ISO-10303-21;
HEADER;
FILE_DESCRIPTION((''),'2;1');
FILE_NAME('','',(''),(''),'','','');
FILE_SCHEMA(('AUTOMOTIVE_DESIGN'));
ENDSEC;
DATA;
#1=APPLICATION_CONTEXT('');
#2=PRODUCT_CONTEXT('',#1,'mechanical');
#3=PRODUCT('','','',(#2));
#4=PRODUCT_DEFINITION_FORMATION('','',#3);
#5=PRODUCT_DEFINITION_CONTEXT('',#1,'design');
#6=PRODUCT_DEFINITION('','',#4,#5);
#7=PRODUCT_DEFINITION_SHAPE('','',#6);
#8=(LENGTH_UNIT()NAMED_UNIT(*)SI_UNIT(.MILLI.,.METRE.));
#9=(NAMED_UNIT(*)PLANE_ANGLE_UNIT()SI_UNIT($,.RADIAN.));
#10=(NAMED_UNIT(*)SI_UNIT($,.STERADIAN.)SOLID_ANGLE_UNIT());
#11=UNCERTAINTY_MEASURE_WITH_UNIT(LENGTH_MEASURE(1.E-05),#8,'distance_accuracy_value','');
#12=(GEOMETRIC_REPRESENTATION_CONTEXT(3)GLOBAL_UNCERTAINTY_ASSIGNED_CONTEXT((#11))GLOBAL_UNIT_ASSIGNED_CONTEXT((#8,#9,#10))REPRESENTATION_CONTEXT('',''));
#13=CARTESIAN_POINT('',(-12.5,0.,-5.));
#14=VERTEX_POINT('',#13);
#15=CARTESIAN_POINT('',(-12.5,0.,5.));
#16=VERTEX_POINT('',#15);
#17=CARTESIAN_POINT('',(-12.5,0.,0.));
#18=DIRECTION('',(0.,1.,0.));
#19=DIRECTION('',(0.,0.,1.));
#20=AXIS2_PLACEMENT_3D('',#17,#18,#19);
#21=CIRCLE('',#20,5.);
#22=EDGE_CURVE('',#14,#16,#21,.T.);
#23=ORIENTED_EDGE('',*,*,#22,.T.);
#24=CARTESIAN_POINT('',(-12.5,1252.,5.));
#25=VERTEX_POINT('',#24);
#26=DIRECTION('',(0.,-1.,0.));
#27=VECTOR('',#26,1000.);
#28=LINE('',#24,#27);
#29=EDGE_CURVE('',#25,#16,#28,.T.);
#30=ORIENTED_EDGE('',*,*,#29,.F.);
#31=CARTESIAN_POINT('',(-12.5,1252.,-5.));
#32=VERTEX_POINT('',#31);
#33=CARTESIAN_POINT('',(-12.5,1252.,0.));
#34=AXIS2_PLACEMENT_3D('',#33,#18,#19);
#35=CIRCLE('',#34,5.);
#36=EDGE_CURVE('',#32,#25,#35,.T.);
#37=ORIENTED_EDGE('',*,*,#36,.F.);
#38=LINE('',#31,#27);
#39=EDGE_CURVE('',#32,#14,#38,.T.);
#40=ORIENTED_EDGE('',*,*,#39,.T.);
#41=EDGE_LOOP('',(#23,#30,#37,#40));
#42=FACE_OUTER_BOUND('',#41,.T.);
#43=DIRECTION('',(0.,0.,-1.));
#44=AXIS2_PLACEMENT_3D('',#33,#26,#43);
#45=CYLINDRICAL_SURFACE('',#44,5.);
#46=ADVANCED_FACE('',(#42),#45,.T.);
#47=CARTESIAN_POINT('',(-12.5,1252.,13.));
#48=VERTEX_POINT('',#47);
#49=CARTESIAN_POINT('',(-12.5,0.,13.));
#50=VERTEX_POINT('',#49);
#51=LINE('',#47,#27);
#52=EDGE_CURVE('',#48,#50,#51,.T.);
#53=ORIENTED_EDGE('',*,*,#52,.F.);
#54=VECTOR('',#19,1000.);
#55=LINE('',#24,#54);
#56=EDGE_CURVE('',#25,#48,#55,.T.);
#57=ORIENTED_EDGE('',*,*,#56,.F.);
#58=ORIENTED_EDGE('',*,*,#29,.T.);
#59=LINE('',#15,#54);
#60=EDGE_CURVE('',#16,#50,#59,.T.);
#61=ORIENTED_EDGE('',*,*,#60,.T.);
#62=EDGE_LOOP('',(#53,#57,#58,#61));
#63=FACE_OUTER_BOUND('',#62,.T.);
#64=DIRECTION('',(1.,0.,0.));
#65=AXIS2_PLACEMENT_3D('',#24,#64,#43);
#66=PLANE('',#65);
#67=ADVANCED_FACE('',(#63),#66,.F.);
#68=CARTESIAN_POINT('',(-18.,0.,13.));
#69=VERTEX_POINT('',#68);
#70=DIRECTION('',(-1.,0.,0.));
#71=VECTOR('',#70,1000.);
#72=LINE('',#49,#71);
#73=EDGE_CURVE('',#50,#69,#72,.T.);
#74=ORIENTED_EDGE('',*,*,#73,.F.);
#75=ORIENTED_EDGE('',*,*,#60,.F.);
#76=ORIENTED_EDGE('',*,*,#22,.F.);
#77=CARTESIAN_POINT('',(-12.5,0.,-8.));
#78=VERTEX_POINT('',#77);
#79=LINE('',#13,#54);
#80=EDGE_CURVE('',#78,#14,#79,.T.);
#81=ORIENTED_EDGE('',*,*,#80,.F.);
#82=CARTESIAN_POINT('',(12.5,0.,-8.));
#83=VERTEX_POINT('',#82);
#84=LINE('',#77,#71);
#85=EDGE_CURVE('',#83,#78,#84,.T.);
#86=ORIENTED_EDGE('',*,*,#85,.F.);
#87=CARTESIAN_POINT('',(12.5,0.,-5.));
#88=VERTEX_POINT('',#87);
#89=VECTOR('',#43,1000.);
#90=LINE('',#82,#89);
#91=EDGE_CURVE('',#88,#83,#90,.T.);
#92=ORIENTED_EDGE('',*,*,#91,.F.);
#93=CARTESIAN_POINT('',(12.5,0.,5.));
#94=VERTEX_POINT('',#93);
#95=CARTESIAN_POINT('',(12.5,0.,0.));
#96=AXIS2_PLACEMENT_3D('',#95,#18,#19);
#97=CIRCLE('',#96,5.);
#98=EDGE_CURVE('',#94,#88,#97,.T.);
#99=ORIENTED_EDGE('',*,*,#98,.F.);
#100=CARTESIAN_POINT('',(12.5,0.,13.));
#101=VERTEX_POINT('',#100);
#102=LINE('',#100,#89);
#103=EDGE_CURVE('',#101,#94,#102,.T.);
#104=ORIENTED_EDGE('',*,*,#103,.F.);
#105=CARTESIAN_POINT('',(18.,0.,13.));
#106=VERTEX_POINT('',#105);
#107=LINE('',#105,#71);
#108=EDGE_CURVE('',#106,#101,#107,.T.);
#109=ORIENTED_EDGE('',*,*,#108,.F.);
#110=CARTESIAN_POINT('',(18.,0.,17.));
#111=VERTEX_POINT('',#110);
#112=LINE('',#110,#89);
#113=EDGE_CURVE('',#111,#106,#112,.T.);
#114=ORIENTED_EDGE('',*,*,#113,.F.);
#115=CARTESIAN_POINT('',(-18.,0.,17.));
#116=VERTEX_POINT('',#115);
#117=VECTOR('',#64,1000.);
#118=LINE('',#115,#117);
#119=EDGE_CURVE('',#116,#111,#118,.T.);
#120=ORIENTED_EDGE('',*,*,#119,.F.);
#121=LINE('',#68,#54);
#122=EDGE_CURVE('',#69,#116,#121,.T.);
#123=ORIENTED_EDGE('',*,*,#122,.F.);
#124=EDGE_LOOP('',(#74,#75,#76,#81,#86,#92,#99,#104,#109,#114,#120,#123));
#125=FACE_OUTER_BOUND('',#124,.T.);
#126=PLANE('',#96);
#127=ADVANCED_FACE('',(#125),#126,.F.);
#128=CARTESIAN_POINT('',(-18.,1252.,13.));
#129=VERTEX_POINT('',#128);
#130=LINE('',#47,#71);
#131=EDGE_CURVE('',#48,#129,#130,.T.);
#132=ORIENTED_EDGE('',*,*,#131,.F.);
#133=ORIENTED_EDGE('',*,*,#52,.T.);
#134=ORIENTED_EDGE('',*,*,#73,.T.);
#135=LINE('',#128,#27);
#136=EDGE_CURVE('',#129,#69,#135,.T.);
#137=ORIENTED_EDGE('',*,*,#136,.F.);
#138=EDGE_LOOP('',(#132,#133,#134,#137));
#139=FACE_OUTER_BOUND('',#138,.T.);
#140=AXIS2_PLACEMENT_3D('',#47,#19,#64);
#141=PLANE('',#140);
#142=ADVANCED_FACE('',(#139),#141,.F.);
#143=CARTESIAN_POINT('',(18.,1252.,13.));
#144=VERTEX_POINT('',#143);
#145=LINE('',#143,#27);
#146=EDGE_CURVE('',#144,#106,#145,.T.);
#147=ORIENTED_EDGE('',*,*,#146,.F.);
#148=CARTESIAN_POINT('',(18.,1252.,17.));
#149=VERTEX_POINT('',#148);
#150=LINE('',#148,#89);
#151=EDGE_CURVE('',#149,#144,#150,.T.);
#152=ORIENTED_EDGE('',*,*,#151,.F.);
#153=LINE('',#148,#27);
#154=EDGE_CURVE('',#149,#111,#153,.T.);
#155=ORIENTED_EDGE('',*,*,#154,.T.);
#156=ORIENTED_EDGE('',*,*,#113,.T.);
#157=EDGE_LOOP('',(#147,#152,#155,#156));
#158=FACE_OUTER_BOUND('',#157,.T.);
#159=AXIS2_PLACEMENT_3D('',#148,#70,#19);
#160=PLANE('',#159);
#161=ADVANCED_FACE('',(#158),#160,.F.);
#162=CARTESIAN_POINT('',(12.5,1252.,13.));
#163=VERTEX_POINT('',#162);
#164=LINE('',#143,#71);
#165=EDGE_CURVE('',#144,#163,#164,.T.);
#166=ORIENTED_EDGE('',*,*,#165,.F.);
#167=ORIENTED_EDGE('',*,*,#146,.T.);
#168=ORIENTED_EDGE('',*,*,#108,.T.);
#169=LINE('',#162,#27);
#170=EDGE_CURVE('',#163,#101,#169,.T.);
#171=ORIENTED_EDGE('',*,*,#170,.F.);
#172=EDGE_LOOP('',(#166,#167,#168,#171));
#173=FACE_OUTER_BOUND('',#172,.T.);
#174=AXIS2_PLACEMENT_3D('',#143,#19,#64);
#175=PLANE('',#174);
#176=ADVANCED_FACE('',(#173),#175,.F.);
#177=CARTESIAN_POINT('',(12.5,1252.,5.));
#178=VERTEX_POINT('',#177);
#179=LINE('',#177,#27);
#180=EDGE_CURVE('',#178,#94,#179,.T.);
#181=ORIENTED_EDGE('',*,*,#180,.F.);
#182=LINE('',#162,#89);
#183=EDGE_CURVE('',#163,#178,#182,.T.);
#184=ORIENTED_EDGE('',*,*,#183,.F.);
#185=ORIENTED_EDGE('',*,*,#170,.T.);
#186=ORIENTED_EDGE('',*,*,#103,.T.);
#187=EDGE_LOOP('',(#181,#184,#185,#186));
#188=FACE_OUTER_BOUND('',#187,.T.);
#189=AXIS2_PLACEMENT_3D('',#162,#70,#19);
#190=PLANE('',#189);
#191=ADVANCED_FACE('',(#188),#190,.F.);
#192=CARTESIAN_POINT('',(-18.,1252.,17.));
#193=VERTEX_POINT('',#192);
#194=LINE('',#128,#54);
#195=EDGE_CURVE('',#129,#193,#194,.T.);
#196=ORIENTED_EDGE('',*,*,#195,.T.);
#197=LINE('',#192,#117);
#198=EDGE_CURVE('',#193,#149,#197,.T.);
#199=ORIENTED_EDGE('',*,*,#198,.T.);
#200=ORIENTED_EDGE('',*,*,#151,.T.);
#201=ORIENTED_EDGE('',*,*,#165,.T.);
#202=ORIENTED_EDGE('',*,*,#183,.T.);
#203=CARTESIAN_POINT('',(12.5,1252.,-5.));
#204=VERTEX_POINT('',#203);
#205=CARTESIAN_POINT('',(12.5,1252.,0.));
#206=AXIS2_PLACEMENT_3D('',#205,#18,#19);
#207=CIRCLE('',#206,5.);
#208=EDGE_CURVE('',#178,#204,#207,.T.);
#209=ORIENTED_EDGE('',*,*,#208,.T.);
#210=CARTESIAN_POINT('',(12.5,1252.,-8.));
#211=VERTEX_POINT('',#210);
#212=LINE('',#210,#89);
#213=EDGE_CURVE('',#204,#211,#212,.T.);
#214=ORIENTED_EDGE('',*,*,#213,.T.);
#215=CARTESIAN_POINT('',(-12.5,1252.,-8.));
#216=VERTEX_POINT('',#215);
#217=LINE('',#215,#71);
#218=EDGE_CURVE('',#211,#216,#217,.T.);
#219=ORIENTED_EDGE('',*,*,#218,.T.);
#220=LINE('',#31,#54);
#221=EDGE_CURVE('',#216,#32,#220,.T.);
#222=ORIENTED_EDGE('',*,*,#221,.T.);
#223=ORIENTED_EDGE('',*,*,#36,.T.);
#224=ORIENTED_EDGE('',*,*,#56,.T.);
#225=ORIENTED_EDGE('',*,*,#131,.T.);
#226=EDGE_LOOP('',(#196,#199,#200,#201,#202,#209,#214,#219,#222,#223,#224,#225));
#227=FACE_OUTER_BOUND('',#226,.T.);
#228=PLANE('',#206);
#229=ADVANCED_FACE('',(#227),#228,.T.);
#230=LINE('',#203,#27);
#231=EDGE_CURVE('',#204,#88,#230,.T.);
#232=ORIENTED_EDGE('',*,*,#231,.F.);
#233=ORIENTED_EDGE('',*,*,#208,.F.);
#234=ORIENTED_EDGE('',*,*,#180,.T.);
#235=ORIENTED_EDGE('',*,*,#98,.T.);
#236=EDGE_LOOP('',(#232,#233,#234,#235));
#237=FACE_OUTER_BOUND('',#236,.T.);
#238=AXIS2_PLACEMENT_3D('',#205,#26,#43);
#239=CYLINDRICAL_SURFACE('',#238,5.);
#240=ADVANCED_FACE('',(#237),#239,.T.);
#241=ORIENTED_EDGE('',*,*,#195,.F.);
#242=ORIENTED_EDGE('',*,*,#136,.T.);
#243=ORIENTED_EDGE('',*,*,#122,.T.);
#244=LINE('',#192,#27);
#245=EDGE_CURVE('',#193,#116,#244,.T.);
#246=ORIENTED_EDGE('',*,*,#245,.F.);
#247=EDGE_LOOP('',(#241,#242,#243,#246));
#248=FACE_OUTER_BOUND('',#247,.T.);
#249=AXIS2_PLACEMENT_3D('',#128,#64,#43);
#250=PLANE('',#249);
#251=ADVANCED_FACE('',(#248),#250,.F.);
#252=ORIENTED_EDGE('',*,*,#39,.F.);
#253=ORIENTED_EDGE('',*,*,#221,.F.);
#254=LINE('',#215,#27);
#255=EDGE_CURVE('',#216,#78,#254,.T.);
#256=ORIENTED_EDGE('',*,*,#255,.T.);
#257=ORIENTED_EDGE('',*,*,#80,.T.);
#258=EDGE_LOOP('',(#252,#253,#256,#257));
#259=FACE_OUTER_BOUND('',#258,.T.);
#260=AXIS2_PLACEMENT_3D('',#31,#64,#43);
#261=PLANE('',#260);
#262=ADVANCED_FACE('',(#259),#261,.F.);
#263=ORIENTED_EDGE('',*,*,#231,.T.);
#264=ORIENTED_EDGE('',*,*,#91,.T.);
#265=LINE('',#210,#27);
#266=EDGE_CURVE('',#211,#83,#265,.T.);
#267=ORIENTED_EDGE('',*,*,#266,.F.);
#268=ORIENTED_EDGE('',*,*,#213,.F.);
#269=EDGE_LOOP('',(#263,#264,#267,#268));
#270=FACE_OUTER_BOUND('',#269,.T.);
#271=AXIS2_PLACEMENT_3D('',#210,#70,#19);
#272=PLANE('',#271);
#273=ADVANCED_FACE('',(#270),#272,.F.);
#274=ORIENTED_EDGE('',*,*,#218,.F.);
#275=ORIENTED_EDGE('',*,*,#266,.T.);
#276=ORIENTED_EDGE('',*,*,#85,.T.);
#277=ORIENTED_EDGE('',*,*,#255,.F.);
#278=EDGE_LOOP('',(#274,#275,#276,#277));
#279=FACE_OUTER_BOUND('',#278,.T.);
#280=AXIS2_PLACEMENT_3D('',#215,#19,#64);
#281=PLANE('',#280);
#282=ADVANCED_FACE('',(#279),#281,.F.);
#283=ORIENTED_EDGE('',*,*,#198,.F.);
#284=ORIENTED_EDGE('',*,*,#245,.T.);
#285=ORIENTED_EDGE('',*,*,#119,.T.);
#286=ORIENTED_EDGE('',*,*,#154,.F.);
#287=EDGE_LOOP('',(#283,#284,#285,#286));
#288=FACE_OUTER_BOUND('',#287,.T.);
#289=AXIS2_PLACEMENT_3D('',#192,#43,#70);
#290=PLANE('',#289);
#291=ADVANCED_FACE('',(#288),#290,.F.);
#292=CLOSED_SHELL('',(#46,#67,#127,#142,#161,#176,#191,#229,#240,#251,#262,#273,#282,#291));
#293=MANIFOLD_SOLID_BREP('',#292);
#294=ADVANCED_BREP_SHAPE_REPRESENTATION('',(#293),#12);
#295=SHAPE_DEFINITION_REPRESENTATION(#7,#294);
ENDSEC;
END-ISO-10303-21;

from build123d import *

# Parameters (mm, degrees)
EXTRUDE_1_DEPTH = 1252


with BuildPart() as part:
    # 草图1 → 凸台-拉伸1 (new body)
    with BuildSketch(Plane(origin=(0, 0, 0), x_dir=(1, 0, 0), z_dir=(0, 1, 0))):
        with BuildLine():
            Line((-12.5, 5), (-12.5, 8))
            Line((-12.5, 8), (12.5, 8))
            Line((12.5, 8), (12.5, 5))
            ThreePointArc((12.5, 5), (17.5, 0), (12.5, -5))
            Line((12.5, -5), (12.5, -13))
            Line((12.5, -13), (18, -13))
            Line((18, -13), (18, -17))
            Line((18, -17), (-18, -17))
            Line((-18, -17), (-18, -13))
            Line((-18, -13), (-12.5, -13))
            Line((-12.5, -13), (-12.5, -5))
            ThreePointArc((-12.5, -5), (-17.5, 0), (-12.5, 5))
        make_face()
    extrude(amount=EXTRUDE_1_DEPTH)


solid = part.part
